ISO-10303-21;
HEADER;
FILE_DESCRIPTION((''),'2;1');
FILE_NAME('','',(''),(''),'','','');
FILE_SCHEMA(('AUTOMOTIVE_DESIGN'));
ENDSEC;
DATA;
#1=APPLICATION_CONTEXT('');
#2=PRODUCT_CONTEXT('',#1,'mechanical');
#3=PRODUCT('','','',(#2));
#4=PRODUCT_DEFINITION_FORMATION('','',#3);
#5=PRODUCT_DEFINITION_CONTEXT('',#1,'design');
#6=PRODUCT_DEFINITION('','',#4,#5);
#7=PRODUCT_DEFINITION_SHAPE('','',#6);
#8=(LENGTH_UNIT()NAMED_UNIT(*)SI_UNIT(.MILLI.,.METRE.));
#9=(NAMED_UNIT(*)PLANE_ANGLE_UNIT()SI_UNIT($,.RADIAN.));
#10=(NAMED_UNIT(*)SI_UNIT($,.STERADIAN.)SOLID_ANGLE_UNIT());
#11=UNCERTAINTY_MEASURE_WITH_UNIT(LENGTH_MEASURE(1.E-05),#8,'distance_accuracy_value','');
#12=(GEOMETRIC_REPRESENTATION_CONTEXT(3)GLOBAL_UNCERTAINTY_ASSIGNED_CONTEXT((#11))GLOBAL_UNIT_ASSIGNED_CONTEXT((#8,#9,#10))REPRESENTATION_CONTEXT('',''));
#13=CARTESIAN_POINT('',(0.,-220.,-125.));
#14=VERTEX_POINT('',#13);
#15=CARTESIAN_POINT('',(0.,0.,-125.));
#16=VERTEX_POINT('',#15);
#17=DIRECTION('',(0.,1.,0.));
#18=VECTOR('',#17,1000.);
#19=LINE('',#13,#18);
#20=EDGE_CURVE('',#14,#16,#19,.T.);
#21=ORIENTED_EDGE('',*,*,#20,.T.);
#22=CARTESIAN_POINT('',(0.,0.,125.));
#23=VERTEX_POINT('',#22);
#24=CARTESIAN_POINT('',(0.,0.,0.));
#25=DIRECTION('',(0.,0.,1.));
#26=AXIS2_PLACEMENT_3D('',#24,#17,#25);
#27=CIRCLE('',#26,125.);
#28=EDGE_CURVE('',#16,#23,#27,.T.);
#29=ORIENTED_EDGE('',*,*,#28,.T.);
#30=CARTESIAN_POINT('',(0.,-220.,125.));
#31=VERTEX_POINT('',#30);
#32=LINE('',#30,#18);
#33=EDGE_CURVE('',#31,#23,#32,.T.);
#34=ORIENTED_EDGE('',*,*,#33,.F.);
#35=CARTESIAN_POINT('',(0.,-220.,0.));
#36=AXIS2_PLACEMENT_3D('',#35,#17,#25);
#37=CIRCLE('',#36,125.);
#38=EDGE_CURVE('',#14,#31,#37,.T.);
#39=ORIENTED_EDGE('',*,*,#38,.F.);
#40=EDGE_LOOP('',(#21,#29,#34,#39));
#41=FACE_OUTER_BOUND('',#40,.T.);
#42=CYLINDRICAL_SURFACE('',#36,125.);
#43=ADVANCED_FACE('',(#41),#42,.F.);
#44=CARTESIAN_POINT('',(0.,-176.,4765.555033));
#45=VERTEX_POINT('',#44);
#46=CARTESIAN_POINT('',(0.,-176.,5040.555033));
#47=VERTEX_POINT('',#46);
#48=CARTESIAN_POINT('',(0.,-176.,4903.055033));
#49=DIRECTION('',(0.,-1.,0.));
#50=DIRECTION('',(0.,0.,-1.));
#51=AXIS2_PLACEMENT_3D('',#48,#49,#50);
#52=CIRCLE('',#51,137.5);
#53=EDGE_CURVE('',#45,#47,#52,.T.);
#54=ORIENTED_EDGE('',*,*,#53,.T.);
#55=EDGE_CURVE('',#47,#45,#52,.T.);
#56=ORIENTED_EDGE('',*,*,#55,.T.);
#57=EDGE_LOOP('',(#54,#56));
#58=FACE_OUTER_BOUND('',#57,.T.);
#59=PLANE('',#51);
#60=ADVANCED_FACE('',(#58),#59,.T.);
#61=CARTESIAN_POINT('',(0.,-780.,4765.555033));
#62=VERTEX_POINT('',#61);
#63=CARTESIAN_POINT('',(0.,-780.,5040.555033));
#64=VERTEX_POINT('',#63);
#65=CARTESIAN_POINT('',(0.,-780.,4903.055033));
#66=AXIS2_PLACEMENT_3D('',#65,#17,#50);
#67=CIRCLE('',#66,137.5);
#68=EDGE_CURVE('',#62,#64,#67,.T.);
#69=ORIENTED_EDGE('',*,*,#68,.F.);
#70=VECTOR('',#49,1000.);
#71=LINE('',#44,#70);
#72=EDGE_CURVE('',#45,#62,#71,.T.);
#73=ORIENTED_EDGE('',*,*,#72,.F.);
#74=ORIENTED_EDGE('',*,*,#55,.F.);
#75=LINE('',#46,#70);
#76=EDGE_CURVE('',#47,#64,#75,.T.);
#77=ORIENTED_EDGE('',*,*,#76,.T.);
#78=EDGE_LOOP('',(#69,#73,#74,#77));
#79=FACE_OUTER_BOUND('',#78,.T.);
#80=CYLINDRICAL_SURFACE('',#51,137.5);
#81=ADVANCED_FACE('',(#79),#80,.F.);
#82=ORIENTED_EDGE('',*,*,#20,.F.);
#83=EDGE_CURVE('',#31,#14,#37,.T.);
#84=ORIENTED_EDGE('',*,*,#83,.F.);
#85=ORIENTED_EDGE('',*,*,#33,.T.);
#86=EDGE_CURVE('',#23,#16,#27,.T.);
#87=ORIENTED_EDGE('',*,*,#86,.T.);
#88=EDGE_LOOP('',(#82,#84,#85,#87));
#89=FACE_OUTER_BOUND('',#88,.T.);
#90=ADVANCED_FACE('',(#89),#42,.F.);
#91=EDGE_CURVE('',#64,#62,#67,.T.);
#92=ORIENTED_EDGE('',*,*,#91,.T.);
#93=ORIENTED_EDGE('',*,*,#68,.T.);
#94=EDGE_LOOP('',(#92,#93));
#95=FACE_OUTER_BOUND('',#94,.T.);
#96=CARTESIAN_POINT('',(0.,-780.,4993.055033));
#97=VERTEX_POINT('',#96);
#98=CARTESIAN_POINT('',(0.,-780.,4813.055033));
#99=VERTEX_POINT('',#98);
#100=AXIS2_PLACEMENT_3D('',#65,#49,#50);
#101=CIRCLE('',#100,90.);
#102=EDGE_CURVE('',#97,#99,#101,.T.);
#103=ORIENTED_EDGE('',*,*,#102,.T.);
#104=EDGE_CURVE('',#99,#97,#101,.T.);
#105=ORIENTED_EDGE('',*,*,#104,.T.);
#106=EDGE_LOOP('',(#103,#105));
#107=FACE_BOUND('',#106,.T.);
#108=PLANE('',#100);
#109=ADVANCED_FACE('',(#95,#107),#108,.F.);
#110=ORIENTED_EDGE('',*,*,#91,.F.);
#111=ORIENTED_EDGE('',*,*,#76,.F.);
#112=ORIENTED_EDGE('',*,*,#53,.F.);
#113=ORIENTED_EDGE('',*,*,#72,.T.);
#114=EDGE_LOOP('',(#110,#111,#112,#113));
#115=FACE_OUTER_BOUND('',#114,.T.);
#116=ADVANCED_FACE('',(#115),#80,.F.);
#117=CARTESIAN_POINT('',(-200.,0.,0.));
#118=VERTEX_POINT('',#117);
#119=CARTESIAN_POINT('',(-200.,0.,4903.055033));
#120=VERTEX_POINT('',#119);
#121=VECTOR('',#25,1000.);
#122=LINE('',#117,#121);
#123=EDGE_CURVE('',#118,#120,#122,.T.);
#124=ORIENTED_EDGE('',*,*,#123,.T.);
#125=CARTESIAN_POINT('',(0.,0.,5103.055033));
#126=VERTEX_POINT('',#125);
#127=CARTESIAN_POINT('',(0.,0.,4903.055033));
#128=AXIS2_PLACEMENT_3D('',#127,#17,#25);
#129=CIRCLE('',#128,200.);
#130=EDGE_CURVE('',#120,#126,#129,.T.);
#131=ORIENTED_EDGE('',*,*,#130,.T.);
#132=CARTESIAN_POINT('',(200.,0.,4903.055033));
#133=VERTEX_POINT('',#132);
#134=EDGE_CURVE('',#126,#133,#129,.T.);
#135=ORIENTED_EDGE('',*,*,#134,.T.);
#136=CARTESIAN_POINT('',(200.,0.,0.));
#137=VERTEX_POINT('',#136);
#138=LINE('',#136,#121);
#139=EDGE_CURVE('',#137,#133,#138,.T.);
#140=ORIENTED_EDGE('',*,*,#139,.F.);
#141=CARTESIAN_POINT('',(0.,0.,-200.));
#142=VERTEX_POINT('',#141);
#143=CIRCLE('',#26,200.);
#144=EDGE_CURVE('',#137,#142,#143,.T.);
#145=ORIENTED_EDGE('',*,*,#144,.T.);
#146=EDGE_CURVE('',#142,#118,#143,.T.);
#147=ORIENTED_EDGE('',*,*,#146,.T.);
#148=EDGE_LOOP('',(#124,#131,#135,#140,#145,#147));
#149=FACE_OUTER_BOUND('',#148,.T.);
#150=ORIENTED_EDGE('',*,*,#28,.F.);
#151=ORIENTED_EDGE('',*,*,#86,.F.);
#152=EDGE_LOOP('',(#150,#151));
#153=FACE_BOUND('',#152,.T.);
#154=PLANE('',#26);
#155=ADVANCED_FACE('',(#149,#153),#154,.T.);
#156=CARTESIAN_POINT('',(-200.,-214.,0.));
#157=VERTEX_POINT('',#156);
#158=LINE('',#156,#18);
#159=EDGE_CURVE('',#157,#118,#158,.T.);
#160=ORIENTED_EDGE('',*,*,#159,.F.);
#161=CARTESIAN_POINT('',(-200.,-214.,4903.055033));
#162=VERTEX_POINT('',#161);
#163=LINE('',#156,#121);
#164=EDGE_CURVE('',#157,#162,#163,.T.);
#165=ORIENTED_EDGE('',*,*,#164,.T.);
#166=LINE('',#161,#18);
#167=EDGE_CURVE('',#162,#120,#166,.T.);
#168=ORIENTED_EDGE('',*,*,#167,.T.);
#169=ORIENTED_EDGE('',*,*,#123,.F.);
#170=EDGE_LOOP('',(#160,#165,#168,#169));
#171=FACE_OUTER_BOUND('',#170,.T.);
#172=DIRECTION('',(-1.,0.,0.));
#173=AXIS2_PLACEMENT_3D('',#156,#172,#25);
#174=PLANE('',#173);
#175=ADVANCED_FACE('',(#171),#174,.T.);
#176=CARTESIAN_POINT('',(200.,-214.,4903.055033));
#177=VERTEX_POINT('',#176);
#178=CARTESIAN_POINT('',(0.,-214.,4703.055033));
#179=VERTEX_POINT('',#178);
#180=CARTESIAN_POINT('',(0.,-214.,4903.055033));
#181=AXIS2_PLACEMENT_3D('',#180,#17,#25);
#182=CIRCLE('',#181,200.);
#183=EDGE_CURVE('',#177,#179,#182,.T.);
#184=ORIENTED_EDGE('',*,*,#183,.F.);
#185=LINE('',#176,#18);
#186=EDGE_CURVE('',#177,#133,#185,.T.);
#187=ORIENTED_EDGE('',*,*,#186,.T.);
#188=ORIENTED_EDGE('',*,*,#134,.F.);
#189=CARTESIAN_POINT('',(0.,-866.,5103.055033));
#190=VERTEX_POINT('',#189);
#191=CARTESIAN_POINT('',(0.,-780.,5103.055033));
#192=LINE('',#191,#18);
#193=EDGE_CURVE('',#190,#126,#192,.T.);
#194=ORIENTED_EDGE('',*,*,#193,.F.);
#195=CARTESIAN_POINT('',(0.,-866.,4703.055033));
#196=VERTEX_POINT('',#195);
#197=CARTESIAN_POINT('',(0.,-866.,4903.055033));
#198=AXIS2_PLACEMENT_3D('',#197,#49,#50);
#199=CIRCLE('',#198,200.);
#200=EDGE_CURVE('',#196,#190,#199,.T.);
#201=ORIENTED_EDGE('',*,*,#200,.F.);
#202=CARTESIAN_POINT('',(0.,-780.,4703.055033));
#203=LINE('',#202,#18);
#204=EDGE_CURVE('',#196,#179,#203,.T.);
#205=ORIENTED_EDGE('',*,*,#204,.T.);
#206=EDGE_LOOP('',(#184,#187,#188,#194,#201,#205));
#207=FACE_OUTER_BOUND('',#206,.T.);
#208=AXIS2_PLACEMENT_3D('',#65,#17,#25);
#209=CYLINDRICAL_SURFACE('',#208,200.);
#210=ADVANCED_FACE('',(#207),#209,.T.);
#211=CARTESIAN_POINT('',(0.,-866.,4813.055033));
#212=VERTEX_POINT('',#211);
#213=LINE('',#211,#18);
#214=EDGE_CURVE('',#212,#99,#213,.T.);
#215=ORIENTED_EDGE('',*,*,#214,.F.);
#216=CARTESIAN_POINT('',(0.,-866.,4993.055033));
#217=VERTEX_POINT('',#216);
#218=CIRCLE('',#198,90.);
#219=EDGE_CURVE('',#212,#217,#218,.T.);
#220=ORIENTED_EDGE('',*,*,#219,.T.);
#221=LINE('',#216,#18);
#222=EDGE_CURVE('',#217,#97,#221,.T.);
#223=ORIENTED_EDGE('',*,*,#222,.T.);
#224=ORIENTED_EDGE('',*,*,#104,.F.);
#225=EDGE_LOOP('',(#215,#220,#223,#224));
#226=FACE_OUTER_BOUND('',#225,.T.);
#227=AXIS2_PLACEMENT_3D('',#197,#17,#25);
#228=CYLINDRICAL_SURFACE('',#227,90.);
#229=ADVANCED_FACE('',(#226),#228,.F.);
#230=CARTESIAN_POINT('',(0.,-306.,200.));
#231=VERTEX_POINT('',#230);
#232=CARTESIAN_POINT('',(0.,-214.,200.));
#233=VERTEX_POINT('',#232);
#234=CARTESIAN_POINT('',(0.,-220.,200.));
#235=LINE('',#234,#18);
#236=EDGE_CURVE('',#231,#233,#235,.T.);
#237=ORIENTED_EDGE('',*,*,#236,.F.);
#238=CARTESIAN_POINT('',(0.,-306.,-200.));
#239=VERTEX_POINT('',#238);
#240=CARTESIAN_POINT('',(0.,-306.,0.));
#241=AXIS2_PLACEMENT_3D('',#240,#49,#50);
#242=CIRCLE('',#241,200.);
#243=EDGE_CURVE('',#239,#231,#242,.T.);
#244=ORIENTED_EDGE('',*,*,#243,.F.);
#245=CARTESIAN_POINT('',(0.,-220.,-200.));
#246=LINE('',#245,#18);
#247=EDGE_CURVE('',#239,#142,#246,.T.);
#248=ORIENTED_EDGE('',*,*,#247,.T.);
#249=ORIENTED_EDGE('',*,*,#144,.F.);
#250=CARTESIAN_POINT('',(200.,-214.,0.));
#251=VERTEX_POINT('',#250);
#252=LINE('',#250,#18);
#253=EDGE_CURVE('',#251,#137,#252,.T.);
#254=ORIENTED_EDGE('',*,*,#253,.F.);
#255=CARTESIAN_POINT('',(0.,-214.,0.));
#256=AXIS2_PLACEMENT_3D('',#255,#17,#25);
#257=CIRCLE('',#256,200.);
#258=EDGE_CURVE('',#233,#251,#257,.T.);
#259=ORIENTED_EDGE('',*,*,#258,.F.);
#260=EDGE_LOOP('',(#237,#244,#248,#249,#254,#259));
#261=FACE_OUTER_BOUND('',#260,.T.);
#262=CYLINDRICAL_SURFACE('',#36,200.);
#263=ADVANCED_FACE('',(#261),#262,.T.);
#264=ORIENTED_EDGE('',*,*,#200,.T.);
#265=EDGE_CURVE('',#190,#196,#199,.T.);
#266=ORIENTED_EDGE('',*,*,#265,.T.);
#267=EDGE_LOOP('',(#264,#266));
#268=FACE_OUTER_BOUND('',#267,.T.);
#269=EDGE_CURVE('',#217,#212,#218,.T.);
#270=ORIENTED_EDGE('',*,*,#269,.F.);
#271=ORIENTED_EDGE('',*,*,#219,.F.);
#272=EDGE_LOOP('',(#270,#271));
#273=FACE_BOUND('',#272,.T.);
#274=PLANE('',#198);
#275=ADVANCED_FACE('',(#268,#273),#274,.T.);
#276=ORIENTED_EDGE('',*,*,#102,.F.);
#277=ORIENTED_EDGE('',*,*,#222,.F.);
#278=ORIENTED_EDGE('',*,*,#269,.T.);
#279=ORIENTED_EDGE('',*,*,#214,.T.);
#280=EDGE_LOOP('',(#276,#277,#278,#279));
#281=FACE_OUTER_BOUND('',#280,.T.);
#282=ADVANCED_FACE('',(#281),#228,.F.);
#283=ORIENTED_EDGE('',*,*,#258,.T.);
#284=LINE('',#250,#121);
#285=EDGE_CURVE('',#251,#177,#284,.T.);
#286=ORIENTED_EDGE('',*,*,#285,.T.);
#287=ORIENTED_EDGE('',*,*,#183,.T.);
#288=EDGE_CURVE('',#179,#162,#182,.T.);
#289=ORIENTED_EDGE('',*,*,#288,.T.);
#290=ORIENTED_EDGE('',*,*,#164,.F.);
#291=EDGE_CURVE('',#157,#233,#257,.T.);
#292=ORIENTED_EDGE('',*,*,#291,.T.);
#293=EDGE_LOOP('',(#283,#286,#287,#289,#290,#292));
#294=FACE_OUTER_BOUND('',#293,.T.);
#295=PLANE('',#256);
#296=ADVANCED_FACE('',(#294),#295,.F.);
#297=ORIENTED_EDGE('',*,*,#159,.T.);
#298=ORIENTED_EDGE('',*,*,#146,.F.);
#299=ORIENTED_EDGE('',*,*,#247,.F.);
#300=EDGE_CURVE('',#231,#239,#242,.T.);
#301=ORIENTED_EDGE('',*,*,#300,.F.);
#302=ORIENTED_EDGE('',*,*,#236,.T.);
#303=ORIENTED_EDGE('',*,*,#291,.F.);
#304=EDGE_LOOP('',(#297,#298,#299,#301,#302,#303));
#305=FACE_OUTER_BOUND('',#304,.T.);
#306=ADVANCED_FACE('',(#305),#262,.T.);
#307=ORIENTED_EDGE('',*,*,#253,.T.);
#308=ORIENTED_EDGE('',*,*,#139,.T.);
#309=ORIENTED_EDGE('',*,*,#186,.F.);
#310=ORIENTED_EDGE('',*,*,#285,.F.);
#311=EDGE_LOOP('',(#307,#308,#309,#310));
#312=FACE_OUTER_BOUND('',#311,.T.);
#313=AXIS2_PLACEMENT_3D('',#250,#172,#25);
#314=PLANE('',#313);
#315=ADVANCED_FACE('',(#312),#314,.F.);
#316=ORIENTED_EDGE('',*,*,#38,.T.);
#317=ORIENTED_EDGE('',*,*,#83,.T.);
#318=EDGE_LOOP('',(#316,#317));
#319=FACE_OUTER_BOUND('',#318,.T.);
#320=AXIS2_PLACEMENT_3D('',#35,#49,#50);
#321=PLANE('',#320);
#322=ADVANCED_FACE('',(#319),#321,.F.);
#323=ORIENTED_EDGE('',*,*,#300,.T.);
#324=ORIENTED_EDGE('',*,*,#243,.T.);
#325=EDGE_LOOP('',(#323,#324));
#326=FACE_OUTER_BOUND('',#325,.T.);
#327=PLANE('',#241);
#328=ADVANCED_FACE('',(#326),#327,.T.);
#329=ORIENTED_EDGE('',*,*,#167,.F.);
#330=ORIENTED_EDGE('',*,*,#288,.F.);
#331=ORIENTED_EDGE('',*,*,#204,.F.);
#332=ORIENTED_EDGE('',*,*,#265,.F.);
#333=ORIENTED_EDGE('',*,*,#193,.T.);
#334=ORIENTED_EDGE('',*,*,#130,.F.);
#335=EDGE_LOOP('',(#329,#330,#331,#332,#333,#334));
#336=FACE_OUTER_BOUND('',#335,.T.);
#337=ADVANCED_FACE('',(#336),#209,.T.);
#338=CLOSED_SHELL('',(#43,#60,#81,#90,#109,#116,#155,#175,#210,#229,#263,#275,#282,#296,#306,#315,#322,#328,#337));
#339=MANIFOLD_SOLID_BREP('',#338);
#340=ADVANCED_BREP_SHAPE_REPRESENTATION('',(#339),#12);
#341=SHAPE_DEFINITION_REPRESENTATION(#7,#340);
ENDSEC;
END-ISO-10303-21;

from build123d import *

# Parameters (mm, degrees)
SKETCH1_R           = 200
SKETCH1_R_2         = 125
BOSS_EXTRUDE1_DEPTH = 220
BOSS_EXTRUDE2_DEPTH = 214
SKETCH3_R           = 200
BOSS_EXTRUDE3_DEPTH = 780
SKETCH4_R           = 137.5
CUT_EXTRUDE1_DEPTH  = 604
SKETCH5_R           = 200
SKETCH5_R_2         = 90
BOSS_EXTRUDE4_DEPTH = 86
SKETCH6_R           = 200
BOSS_EXTRUDE5_DEPTH = 86


with BuildPart() as part:
    # Sketch1 → Boss-Extrude1 (new body)
    with BuildSketch(Plane(origin=(0, 0, 0), x_dir=(1, 0, 0), z_dir=(0, 1, 0))):
        with Locations(Location((0, 0, 0), (0, 0, 270))):
            Circle(SKETCH1_R)
        with Locations(Location((0, 0, 0), (0, 0, 270))):
            Circle(SKETCH1_R_2, mode=Mode.SUBTRACT)
    extrude(amount=-BOSS_EXTRUDE1_DEPTH)

    # Sketch2 → Boss-Extrude2 (add)
    with BuildSketch(Plane(origin=(0, 0, 0), x_dir=(1, 0, 0), z_dir=(0, 1, 0))):
        with BuildLine():
            ThreePointArc((200, 0), (0, -200), (-200, 0))
            Line((-200, 0), (-200, -4903.05503267))
            ThreePointArc((-200, -4903.05503267), (0, -4703.05503267), (200, -4903.05503267))
            Line((200, -4903.05503267), (200, 0))
        make_face()
    extrude(amount=-BOSS_EXTRUDE2_DEPTH)

    # Sketch3 → Boss-Extrude3 (add)
    with BuildSketch(Plane(origin=(0, 0, 0), x_dir=(1, 0, 0), z_dir=(0, 1, 0))):
        with Locations(Location((0, -4903.05503267, 0), (0, 0, 270))):
            Circle(SKETCH3_R)
    extrude(amount=-BOSS_EXTRUDE3_DEPTH)

    # Sketch4 → Cut-Extrude1 (cut)
    with BuildSketch(Plane.XZ.offset(780)):
        with Locations(Location((0, 4903.05503267, 0), (0, 0, 270))):
            Circle(SKETCH4_R)
    extrude(amount=-CUT_EXTRUDE1_DEPTH, mode=Mode.SUBTRACT)

    # Sketch5 → Boss-Extrude4 (add)
    with BuildSketch(Plane.XZ.offset(780)):
        with Locations((0, 4903.05503267)):
            Circle(SKETCH5_R)
        with Locations(Location((0, 4903.05503267, 0), (0, 0, 270))):
            Circle(SKETCH5_R_2, mode=Mode.SUBTRACT)
    extrude(amount=BOSS_EXTRUDE4_DEPTH)

    # Sketch6 → Boss-Extrude5 (add)
    with BuildSketch(Plane.XZ.offset(220)):
        Circle(SKETCH6_R)
    extrude(amount=BOSS_EXTRUDE5_DEPTH)


solid = part.part
